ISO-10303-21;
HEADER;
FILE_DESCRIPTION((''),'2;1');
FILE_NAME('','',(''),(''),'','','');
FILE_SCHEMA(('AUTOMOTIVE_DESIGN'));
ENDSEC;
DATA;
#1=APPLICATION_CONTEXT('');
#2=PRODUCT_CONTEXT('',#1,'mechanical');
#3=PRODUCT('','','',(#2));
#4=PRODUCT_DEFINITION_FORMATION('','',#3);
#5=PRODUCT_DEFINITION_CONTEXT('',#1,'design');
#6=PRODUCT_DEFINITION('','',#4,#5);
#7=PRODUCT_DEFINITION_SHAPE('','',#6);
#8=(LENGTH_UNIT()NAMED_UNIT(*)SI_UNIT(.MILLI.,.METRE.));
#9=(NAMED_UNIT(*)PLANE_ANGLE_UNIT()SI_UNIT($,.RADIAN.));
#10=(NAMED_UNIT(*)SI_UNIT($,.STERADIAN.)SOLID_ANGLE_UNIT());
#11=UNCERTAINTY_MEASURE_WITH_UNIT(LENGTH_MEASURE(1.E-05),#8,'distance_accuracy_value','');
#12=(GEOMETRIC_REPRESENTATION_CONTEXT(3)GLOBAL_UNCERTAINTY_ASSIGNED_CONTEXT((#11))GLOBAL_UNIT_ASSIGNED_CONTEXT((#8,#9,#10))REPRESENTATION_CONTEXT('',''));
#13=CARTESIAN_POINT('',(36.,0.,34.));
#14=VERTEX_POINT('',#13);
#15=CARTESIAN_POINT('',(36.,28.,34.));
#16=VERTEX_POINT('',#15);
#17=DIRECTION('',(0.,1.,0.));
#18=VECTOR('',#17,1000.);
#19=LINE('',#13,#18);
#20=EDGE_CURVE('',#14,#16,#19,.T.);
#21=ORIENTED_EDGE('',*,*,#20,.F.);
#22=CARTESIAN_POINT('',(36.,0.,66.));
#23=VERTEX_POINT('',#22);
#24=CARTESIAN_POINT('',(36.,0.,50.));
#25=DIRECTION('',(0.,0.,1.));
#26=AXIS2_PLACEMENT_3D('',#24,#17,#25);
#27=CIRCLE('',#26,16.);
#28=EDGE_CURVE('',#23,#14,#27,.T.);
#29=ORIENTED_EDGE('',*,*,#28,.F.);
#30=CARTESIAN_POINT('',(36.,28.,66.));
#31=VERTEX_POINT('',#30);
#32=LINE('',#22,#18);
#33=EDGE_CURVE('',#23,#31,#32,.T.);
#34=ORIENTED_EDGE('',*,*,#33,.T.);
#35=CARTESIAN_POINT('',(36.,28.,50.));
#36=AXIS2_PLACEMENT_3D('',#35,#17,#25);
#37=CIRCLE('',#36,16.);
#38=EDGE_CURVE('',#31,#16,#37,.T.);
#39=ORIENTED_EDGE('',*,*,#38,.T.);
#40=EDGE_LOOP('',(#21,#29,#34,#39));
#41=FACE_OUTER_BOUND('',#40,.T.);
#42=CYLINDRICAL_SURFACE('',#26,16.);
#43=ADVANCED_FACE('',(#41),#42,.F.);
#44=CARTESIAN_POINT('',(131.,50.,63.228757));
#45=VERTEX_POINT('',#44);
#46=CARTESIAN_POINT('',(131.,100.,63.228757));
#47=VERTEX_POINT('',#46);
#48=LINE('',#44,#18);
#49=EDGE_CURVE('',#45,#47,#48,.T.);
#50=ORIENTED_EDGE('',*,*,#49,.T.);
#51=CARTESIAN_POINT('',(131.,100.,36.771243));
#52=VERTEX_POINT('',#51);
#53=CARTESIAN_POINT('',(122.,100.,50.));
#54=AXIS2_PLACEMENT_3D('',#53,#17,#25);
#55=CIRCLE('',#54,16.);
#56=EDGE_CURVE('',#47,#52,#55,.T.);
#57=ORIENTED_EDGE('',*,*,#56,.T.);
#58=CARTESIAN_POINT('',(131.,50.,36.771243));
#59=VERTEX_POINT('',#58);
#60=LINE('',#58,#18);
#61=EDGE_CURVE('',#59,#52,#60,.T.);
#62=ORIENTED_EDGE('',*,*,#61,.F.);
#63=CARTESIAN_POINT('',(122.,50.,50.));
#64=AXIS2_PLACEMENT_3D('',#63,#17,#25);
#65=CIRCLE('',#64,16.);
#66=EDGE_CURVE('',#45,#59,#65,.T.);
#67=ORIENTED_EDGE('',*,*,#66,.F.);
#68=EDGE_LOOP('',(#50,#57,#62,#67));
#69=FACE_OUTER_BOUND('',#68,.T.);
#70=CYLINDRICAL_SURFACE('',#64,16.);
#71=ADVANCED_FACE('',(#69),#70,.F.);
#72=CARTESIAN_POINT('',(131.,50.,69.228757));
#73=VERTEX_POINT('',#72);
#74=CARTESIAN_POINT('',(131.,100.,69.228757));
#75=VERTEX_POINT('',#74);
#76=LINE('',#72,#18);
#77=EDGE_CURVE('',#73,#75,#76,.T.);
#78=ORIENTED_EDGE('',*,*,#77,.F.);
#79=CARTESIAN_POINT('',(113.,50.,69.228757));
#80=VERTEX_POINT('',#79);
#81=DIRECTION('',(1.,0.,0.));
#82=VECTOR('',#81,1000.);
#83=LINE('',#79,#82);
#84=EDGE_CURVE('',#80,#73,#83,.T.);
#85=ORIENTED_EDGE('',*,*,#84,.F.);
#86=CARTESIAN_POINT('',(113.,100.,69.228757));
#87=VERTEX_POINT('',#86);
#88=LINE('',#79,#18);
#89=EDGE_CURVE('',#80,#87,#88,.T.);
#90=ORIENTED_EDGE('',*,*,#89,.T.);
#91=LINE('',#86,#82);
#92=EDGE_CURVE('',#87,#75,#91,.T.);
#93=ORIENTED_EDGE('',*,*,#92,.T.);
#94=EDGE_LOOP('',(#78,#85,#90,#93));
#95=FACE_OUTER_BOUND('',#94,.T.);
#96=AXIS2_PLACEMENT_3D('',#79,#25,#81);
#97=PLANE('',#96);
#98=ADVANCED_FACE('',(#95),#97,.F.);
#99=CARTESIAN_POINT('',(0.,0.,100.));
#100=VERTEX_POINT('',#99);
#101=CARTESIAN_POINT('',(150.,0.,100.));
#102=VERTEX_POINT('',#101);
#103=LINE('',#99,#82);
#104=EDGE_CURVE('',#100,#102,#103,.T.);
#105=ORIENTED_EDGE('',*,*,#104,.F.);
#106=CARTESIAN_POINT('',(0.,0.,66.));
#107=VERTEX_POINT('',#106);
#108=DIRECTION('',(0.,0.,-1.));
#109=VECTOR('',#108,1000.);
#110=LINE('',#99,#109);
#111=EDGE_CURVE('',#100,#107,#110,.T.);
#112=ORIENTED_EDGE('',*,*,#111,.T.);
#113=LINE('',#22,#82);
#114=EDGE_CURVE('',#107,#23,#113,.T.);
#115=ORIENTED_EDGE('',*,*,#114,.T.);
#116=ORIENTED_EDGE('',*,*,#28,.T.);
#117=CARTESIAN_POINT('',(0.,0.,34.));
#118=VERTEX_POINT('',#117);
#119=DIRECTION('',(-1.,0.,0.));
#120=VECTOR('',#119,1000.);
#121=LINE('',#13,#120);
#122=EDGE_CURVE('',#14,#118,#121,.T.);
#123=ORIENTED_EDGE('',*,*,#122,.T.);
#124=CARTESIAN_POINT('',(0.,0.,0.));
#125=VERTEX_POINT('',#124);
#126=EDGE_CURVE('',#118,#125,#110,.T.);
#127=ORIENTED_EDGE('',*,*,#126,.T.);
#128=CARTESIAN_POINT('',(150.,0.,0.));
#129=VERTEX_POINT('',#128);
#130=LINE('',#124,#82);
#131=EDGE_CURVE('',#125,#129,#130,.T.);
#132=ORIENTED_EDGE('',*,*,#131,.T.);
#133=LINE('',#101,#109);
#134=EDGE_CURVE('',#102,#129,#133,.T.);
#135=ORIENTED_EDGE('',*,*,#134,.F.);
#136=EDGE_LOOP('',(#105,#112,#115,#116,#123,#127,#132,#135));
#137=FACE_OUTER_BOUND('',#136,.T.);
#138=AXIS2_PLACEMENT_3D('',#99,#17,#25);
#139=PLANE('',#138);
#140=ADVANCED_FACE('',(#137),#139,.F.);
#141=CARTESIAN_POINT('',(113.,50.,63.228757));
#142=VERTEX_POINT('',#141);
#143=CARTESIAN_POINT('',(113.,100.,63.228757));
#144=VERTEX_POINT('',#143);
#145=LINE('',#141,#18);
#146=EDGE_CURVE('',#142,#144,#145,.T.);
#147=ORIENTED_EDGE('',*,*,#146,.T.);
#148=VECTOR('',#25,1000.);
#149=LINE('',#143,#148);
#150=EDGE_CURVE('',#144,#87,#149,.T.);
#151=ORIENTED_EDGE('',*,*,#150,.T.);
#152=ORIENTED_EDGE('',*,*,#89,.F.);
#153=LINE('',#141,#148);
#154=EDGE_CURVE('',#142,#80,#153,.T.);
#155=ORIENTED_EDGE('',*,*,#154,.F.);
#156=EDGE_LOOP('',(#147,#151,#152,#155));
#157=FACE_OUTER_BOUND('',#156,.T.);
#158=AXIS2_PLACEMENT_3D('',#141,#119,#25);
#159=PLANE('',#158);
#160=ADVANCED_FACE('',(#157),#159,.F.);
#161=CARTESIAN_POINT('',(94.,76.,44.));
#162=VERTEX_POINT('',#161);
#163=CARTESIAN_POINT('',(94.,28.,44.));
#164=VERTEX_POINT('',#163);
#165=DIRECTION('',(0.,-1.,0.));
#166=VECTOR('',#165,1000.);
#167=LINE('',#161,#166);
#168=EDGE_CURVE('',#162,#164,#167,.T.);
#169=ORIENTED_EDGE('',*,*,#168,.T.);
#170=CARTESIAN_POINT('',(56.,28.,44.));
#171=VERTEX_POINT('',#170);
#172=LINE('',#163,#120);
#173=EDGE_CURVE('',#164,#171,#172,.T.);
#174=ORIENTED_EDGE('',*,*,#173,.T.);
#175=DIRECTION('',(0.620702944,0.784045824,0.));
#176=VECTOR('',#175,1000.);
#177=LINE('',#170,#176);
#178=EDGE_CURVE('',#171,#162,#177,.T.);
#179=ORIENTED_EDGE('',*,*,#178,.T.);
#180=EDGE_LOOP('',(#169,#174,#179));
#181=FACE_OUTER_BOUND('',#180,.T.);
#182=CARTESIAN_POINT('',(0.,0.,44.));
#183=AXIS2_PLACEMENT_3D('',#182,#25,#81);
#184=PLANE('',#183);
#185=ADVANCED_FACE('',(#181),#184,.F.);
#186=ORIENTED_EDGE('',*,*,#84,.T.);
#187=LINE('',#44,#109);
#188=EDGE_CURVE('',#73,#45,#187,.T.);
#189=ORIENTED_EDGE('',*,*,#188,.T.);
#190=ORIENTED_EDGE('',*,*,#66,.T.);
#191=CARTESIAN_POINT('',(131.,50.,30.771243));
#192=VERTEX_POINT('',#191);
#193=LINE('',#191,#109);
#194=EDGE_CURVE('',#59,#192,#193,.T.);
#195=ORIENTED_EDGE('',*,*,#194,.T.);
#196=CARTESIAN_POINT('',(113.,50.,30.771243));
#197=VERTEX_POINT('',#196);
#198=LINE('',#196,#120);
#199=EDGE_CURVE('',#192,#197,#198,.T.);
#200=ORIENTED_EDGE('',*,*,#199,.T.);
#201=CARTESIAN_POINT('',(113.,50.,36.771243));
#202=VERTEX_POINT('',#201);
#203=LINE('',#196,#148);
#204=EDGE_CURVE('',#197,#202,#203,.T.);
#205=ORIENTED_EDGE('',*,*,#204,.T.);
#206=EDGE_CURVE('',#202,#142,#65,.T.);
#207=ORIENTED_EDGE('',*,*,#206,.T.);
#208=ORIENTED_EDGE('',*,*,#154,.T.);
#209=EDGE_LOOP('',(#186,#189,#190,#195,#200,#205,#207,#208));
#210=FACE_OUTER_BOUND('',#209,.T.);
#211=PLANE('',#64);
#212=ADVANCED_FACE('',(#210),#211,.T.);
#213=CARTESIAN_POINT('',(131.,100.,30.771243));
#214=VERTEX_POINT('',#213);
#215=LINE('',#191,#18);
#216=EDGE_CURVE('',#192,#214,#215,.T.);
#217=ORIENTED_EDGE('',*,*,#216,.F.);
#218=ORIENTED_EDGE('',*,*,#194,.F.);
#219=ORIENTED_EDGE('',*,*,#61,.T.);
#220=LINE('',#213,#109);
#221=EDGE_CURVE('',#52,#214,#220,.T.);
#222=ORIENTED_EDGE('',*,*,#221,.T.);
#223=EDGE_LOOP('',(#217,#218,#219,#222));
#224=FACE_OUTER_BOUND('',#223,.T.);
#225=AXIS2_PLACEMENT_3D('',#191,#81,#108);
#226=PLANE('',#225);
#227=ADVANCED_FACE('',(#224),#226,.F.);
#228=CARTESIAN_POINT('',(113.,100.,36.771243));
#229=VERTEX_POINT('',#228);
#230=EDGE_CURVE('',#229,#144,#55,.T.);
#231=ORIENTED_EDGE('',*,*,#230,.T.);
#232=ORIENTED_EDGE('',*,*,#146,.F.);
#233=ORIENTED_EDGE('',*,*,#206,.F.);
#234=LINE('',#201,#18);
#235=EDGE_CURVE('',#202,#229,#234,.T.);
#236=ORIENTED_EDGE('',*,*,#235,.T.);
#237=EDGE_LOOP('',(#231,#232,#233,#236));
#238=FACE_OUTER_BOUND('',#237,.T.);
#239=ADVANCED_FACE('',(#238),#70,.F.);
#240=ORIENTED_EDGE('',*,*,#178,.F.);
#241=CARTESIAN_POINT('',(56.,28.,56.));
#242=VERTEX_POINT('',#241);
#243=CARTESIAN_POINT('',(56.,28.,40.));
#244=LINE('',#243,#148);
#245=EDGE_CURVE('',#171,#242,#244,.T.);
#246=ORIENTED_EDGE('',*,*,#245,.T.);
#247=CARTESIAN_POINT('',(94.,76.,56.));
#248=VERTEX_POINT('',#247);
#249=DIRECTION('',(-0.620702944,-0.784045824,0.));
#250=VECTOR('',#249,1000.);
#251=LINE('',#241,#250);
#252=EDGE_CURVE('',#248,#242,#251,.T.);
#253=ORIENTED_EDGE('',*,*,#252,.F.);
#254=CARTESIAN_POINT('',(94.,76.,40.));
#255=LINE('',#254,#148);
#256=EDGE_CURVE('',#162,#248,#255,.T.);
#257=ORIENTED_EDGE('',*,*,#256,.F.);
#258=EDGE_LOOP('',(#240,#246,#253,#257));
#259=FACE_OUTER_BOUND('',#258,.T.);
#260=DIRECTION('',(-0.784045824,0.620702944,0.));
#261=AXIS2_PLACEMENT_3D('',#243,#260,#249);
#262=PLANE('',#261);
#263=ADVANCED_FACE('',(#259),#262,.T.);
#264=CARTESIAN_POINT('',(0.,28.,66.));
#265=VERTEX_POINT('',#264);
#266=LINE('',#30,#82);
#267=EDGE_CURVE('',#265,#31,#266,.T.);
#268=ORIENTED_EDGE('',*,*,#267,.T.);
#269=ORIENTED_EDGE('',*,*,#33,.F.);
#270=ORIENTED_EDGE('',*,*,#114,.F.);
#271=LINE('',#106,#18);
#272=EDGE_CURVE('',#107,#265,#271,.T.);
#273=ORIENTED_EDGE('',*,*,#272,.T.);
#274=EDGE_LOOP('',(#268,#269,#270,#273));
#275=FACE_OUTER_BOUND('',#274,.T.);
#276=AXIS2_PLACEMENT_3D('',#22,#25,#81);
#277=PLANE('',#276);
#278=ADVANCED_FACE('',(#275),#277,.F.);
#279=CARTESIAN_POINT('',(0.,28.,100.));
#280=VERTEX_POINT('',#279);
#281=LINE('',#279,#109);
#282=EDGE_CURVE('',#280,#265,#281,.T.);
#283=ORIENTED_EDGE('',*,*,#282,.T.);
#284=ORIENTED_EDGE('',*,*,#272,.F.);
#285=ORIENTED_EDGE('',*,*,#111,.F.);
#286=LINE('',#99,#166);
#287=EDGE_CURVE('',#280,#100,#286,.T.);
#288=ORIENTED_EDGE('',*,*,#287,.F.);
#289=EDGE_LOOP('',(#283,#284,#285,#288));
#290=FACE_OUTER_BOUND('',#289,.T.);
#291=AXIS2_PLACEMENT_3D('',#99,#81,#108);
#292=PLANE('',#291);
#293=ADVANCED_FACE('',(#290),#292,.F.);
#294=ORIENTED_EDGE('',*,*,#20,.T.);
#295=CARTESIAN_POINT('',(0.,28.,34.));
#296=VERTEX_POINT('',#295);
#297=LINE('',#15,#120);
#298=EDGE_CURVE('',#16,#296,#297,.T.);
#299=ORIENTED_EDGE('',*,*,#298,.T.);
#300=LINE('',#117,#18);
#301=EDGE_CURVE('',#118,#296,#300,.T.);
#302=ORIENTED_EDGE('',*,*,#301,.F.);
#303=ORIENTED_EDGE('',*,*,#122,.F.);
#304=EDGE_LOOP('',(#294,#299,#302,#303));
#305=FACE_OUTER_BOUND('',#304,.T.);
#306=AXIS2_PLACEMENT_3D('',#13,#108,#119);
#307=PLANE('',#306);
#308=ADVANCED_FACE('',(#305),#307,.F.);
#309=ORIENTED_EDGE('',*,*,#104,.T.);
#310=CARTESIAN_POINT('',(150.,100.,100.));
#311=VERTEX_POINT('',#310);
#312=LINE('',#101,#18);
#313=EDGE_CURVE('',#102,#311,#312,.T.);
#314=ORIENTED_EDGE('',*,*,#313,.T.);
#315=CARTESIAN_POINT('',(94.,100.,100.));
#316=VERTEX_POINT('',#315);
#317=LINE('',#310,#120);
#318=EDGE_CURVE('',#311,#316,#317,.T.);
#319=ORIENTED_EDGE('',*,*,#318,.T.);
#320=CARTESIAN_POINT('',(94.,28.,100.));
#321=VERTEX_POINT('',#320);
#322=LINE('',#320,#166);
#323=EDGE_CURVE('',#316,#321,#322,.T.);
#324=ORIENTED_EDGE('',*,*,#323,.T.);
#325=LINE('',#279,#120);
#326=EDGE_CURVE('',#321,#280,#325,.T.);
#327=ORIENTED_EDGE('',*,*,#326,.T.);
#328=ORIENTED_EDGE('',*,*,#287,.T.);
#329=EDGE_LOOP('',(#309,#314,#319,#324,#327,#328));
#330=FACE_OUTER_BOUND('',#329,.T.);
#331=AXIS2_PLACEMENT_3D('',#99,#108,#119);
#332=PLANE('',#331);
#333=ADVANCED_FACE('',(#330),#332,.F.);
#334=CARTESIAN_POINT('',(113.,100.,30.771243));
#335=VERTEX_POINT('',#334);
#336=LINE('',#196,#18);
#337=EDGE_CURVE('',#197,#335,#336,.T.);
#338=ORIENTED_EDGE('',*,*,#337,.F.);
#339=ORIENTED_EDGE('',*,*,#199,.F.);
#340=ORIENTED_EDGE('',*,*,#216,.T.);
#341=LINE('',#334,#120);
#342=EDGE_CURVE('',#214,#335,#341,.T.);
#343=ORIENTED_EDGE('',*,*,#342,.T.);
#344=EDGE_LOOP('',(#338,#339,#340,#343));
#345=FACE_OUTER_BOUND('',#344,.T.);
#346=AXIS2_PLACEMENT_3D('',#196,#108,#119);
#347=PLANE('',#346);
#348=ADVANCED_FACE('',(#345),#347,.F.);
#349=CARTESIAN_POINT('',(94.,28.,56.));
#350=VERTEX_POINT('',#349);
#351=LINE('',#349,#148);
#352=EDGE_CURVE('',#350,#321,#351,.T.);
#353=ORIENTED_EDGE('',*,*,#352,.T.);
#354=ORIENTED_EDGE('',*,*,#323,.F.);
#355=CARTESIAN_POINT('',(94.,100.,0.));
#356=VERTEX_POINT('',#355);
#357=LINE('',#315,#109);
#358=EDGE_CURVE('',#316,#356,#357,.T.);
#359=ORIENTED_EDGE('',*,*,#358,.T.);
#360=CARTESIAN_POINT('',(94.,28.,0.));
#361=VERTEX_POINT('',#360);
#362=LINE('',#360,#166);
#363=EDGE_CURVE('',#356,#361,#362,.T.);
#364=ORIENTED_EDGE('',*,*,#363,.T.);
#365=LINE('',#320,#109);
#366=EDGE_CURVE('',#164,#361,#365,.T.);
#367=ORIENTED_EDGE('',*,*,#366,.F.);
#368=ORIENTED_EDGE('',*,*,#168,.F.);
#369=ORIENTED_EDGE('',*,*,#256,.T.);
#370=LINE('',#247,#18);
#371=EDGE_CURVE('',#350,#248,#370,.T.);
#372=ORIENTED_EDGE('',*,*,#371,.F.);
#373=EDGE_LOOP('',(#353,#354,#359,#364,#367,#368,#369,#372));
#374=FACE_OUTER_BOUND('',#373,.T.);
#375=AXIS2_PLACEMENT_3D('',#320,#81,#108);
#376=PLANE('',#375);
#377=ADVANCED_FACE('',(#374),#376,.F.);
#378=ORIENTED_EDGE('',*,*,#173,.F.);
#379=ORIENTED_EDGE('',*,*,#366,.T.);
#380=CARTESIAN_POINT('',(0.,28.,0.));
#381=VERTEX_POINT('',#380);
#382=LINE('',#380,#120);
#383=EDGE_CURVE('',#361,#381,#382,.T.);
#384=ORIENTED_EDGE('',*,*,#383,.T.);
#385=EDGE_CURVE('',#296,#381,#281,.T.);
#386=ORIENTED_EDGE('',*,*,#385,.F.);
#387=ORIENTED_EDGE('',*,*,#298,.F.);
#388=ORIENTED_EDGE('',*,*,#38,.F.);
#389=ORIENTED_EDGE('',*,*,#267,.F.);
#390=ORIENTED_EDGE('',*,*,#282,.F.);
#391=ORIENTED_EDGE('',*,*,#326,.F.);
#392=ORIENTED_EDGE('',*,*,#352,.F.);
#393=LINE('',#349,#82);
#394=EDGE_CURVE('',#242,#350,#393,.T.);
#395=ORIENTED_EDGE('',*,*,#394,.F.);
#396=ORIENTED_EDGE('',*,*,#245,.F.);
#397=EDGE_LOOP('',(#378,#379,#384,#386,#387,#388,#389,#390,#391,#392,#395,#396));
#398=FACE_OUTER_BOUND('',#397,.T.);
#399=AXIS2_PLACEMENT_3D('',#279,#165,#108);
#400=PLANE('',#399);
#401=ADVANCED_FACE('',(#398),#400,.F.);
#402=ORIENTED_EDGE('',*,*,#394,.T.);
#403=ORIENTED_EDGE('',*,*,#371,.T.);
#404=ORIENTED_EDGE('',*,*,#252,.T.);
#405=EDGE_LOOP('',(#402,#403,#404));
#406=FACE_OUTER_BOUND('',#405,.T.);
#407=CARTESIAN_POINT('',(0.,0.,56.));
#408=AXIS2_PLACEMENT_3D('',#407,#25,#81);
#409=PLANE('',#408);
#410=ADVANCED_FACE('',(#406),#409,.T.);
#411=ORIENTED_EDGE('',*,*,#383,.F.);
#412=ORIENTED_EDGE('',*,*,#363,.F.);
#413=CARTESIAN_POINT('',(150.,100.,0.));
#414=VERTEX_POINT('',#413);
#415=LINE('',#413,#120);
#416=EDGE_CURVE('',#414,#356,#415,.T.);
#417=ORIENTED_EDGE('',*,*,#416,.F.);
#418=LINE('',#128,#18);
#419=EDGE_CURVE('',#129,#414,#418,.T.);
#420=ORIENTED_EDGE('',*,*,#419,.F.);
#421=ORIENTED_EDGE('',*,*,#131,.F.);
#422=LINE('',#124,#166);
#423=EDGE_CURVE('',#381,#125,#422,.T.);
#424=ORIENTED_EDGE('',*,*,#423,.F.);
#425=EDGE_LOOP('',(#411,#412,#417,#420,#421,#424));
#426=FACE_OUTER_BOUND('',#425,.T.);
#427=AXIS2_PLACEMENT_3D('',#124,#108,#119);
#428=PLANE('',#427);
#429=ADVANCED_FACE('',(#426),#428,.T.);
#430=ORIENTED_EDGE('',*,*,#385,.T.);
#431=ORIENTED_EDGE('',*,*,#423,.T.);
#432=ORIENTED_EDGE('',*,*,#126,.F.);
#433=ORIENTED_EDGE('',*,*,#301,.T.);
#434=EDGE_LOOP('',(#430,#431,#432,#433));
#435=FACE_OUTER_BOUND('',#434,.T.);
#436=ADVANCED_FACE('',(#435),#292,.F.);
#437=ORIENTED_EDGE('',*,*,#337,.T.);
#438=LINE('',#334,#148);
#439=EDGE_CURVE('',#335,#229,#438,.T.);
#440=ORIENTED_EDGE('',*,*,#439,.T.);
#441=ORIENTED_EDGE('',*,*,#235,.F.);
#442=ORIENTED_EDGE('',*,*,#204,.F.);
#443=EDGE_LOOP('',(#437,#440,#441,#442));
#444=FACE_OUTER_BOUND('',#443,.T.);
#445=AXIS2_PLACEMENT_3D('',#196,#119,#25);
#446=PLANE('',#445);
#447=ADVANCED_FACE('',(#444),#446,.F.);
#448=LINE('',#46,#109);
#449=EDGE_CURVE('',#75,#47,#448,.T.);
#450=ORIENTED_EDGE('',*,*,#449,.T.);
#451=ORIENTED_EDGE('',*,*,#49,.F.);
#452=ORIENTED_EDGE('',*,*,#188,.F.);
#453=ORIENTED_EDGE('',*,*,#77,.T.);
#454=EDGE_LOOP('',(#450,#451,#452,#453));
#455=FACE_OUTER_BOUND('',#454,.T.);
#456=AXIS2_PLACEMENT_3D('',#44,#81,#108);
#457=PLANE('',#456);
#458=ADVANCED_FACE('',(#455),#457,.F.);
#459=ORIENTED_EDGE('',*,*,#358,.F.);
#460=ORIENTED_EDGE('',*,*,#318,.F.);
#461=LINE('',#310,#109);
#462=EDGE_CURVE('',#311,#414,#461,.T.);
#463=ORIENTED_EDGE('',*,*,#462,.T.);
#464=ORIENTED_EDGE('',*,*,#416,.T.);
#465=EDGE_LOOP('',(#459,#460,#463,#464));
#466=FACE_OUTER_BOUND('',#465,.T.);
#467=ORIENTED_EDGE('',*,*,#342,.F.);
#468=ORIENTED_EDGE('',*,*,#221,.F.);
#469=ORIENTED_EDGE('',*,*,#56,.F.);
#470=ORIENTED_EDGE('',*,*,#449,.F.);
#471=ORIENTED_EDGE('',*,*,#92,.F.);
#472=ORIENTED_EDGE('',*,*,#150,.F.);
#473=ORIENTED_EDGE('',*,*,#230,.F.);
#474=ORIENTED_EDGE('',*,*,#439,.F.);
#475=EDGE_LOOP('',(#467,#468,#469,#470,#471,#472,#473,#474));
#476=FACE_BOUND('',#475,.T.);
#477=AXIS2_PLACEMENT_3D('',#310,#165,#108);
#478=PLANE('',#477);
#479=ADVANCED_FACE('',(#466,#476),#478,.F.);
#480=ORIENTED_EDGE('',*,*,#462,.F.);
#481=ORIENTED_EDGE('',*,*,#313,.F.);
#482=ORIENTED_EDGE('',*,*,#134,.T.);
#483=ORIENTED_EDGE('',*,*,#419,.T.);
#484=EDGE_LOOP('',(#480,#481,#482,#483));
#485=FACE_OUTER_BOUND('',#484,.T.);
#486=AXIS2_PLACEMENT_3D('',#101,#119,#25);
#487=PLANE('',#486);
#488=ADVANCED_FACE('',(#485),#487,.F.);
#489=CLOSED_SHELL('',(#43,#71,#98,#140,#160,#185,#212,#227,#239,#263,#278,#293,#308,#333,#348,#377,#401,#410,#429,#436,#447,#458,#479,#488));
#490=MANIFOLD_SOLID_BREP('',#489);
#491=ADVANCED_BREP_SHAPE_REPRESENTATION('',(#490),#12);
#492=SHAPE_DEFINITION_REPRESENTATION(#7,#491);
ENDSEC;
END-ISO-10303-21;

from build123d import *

# Parameters (mm, degrees)
L_BLOCK_BASE_DEPTH      = 100
KEYED_BORE_CUT_DEPTH    = 50
STEP_BOSS_DEPTH         = 60
STEP_CUT_DEPTH          = 44
STEP_RELIEF_CUT_DEPTH   = 4
LOW_STEP_SLOT_CUT_DEPTH = 28


with BuildPart() as part:
    # L-Block Profile Sketch → L-Block Base (new body)
    with BuildSketch(Plane.XY):
        Polygon((0, 0), (150, 0), (150, 100), (94, 100), (94, 28), (0, 28), align=None)
    extrude(amount=L_BLOCK_BASE_DEPTH)

    # Keyed Bore Sketch → Keyed Bore Cut (cut)
    with BuildSketch(Plane(origin=(0, 100, 0), x_dir=(1, 0, 0), z_dir=(0, 1, 0))):
        with BuildLine():
            Line((113, -69.228756555), (131, -69.228756555))
            Line((131, -69.228756555), (131, -63.228756555))
            ThreePointArc((131, -63.228756555), (138, -50), (131, -36.771243445))
            Line((131, -36.771243445), (131, -30.771243445))
            Line((131, -30.771243445), (113, -30.771243445))
            Line((113, -30.771243445), (113, -36.771243445))
            ThreePointArc((113, -36.771243445), (106, -50), (113, -63.228756555))
            Line((113, -63.228756555), (113, -69.228756555))
        make_face()
    extrude(amount=-KEYED_BORE_CUT_DEPTH, mode=Mode.SUBTRACT)

    # Step Boss Sketch → Step Boss (add)
    with BuildSketch(Plane.XY.offset(100)):
        Polygon((94, 28), (94, 76), (56, 28), align=None)
    extrude(amount=-STEP_BOSS_DEPTH)

    # Step Cut Sketch → Step Cut (cut)
    with BuildSketch(Plane.XY.offset(100)):
        Polygon((94, 76), (94, 28), (56, 28), align=None)
    extrude(amount=-STEP_CUT_DEPTH, mode=Mode.SUBTRACT)

    # Step Relief Sketch → Step Relief Cut (cut)
    with BuildSketch(Plane(origin=(0, 0, 40), x_dir=(-1, 0, 0), z_dir=(0, 0, -1))):
        Polygon((-94, 76), (-94, 28), (-56, 28), align=None)
    extrude(amount=-STEP_RELIEF_CUT_DEPTH, mode=Mode.SUBTRACT)

    # Low Step Slot Sketch → Low Step Slot Cut (cut)
    with BuildSketch(Plane(origin=(0, 28, 0), x_dir=(1, 0, 0), z_dir=(0, 1, 0))):
        with BuildLine():
            Line((0, -34), (0, -66))
            Line((0, -66), (36, -66))
            ThreePointArc((36, -66), (52, -50), (36, -34))
            Line((36, -34), (0, -34))
        make_face()
    extrude(amount=-LOW_STEP_SLOT_CUT_DEPTH, mode=Mode.SUBTRACT)


solid = part.part
